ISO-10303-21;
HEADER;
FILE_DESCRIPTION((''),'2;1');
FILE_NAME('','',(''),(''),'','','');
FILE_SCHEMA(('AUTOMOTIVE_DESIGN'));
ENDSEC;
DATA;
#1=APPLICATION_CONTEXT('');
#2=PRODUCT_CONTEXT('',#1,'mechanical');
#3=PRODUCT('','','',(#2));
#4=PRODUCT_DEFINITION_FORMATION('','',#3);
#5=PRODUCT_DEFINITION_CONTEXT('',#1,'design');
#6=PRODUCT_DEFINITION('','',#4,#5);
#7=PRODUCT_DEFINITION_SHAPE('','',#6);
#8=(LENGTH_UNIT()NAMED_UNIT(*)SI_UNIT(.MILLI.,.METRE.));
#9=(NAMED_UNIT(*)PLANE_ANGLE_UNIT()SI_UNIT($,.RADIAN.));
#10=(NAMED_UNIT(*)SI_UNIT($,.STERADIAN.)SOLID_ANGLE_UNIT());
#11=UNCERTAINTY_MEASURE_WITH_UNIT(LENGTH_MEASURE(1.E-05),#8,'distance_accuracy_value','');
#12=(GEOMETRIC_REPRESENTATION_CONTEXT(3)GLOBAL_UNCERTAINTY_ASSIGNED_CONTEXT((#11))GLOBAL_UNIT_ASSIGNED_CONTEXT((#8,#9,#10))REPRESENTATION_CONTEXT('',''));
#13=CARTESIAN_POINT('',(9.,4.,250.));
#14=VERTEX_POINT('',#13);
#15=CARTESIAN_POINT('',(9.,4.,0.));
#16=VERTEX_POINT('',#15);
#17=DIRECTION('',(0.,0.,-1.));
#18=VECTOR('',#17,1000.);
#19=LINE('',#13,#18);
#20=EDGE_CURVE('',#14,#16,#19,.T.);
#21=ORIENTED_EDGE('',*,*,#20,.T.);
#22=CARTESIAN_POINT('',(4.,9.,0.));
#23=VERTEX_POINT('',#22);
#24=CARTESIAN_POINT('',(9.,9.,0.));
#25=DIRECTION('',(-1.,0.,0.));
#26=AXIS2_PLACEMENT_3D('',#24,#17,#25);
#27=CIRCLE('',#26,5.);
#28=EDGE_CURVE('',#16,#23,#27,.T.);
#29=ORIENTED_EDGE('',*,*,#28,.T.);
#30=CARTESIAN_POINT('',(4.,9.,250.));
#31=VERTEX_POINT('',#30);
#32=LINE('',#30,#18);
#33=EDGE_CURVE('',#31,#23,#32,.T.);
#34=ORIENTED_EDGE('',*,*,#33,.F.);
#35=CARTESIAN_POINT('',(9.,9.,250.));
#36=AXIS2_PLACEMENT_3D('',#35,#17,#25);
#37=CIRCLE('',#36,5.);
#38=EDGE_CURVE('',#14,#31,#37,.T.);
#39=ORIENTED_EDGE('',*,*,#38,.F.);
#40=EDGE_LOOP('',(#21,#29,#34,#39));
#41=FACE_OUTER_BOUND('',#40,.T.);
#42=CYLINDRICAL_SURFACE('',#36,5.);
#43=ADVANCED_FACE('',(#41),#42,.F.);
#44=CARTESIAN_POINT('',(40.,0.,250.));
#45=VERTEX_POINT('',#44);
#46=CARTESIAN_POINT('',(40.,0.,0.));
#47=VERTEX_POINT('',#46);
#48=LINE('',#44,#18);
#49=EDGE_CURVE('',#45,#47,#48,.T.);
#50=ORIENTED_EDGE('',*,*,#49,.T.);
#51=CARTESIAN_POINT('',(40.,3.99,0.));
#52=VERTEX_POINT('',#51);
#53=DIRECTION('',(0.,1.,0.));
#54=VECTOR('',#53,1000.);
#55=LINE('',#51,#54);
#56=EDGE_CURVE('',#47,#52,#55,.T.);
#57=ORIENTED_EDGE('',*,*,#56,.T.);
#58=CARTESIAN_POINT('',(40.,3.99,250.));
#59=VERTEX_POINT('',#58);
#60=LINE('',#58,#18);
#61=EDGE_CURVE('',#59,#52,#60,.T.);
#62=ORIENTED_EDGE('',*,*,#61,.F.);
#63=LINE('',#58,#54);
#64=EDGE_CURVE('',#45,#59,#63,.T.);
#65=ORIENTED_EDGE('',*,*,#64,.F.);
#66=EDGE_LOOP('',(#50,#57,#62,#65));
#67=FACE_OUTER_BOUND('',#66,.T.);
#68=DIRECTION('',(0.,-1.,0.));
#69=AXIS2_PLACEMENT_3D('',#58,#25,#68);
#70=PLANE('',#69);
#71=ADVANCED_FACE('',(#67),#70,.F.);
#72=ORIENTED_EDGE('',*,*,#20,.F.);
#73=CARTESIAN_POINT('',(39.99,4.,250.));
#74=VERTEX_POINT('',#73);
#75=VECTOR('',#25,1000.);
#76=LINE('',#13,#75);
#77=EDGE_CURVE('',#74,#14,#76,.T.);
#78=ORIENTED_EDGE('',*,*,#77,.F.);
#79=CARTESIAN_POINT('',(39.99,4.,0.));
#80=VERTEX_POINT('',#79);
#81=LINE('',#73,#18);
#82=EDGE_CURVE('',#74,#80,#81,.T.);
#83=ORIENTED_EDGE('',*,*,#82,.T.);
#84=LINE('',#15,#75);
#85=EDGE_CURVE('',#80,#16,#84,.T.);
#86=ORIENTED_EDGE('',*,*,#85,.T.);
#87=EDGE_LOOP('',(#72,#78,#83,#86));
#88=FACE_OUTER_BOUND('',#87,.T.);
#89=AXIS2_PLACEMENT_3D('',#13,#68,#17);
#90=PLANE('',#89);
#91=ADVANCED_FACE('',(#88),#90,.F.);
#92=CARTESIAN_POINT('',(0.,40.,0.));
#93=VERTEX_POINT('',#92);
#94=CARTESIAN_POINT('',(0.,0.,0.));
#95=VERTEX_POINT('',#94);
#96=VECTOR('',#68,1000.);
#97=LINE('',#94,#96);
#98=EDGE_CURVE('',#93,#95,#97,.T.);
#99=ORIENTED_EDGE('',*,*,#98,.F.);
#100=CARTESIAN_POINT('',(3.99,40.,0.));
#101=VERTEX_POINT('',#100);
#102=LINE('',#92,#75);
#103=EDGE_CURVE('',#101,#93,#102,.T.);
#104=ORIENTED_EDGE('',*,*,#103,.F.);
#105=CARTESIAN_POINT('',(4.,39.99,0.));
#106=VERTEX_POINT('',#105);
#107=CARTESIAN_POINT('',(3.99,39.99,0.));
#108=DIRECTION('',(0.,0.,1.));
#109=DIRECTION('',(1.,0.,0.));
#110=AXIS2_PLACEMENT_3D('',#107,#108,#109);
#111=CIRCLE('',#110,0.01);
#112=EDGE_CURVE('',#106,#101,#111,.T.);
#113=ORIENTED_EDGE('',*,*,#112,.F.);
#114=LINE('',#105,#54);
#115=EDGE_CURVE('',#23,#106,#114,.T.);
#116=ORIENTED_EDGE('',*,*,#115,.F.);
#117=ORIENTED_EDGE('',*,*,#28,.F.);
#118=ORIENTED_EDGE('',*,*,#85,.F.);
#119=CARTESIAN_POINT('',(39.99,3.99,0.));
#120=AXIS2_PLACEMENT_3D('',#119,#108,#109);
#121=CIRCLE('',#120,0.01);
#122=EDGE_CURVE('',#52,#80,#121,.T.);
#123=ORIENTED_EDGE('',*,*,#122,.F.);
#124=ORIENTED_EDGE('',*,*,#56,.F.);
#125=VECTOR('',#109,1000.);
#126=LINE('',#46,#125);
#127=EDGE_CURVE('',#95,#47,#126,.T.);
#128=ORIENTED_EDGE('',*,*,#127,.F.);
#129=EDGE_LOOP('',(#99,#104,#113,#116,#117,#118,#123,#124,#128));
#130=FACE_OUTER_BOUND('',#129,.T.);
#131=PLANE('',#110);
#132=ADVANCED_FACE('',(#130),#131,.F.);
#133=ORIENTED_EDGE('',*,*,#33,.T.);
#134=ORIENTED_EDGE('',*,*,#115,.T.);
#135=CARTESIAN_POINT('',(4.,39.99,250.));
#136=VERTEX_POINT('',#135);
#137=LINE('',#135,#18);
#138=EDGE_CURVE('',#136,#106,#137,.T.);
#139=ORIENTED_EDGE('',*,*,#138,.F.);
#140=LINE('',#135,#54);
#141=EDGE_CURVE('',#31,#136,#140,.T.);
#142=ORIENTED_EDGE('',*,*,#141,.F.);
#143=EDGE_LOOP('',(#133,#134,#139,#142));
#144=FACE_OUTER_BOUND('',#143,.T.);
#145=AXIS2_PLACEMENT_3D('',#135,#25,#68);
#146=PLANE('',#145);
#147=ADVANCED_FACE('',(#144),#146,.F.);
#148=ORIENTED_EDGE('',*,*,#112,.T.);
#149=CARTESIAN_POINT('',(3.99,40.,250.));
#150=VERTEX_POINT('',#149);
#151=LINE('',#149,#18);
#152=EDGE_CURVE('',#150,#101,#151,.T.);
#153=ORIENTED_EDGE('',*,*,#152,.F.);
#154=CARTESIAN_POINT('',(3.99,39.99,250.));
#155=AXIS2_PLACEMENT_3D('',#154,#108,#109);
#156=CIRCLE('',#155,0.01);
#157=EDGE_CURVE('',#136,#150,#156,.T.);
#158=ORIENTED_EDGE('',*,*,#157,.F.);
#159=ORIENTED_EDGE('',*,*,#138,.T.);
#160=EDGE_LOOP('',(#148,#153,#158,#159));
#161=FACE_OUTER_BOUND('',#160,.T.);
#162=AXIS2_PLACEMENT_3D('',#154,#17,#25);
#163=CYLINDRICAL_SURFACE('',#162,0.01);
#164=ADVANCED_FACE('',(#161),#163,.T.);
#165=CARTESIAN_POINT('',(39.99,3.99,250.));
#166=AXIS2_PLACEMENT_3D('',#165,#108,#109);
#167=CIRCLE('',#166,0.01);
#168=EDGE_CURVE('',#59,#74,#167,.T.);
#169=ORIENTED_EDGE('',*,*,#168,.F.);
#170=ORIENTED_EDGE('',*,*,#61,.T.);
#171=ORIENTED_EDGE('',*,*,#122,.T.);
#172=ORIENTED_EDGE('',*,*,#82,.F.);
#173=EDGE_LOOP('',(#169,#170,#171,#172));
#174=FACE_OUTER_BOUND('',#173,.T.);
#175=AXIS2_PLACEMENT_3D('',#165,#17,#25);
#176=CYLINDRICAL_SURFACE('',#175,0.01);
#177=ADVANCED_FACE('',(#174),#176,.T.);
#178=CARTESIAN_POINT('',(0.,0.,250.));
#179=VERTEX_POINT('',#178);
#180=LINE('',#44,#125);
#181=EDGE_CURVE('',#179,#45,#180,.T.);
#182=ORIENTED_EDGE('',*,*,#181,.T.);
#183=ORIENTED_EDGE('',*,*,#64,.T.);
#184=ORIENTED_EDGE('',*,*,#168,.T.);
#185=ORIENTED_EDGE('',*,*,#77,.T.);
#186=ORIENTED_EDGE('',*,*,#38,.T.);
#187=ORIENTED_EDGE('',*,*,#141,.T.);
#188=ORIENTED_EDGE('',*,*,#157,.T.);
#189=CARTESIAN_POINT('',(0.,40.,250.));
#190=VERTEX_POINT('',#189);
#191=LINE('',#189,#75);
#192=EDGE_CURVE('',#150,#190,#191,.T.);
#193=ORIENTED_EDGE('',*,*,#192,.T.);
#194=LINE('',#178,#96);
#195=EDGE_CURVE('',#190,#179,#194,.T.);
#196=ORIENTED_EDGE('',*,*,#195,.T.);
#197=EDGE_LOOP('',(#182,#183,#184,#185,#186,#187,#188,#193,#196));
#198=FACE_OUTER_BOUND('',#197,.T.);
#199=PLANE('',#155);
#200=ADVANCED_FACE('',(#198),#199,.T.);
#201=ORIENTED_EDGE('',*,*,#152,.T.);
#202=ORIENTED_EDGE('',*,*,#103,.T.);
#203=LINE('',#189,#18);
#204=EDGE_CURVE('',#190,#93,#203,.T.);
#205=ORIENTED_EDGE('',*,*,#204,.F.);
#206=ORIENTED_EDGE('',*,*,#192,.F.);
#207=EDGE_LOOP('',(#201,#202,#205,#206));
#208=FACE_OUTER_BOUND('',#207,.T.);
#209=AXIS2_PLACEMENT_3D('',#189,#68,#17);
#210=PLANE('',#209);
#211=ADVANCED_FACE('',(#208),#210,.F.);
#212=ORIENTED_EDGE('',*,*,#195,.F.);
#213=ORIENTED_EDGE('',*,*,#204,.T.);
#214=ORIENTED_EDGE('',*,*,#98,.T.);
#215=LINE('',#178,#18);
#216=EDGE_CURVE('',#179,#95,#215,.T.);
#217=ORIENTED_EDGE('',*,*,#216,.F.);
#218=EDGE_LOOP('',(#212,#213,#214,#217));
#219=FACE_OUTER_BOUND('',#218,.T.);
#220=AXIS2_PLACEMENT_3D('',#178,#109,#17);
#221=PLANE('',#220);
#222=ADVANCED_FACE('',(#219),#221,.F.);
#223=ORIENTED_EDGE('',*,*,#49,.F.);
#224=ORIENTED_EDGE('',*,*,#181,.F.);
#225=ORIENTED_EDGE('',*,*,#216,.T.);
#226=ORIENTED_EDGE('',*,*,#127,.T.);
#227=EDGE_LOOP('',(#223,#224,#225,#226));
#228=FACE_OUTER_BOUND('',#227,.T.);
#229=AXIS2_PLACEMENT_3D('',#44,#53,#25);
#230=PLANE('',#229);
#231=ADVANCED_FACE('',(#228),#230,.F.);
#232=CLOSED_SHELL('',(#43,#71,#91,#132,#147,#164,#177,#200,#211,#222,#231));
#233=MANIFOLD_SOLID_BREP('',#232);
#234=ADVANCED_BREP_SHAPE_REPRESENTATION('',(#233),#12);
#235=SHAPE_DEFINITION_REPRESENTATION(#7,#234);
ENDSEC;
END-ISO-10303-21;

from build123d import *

# Parameters (mm, degrees)
EXTRUDE_1_DEPTH = 250


with BuildPart() as part:
    # 草图1 → 拉伸1 (new body)
    with BuildSketch(Plane.XY):
        with BuildLine():
            Line((0, 0), (0, 40))
            Line((0, 40), (3.99, 40))
            ThreePointArc((3.99, 40), (3.997071068, 39.997071068), (4, 39.99))
            Line((4, 39.99), (4, 9))
            ThreePointArc((4, 9), (5.464466094, 5.464466094), (9, 4))
            Line((9, 4), (39.99, 4))
            ThreePointArc((39.99, 4), (39.997071068, 3.997071068), (40, 3.99))
            Line((40, 3.99), (40, 0))
            Line((40, 0), (0, 0))
        make_face()
    extrude(amount=EXTRUDE_1_DEPTH)


solid = part.part
